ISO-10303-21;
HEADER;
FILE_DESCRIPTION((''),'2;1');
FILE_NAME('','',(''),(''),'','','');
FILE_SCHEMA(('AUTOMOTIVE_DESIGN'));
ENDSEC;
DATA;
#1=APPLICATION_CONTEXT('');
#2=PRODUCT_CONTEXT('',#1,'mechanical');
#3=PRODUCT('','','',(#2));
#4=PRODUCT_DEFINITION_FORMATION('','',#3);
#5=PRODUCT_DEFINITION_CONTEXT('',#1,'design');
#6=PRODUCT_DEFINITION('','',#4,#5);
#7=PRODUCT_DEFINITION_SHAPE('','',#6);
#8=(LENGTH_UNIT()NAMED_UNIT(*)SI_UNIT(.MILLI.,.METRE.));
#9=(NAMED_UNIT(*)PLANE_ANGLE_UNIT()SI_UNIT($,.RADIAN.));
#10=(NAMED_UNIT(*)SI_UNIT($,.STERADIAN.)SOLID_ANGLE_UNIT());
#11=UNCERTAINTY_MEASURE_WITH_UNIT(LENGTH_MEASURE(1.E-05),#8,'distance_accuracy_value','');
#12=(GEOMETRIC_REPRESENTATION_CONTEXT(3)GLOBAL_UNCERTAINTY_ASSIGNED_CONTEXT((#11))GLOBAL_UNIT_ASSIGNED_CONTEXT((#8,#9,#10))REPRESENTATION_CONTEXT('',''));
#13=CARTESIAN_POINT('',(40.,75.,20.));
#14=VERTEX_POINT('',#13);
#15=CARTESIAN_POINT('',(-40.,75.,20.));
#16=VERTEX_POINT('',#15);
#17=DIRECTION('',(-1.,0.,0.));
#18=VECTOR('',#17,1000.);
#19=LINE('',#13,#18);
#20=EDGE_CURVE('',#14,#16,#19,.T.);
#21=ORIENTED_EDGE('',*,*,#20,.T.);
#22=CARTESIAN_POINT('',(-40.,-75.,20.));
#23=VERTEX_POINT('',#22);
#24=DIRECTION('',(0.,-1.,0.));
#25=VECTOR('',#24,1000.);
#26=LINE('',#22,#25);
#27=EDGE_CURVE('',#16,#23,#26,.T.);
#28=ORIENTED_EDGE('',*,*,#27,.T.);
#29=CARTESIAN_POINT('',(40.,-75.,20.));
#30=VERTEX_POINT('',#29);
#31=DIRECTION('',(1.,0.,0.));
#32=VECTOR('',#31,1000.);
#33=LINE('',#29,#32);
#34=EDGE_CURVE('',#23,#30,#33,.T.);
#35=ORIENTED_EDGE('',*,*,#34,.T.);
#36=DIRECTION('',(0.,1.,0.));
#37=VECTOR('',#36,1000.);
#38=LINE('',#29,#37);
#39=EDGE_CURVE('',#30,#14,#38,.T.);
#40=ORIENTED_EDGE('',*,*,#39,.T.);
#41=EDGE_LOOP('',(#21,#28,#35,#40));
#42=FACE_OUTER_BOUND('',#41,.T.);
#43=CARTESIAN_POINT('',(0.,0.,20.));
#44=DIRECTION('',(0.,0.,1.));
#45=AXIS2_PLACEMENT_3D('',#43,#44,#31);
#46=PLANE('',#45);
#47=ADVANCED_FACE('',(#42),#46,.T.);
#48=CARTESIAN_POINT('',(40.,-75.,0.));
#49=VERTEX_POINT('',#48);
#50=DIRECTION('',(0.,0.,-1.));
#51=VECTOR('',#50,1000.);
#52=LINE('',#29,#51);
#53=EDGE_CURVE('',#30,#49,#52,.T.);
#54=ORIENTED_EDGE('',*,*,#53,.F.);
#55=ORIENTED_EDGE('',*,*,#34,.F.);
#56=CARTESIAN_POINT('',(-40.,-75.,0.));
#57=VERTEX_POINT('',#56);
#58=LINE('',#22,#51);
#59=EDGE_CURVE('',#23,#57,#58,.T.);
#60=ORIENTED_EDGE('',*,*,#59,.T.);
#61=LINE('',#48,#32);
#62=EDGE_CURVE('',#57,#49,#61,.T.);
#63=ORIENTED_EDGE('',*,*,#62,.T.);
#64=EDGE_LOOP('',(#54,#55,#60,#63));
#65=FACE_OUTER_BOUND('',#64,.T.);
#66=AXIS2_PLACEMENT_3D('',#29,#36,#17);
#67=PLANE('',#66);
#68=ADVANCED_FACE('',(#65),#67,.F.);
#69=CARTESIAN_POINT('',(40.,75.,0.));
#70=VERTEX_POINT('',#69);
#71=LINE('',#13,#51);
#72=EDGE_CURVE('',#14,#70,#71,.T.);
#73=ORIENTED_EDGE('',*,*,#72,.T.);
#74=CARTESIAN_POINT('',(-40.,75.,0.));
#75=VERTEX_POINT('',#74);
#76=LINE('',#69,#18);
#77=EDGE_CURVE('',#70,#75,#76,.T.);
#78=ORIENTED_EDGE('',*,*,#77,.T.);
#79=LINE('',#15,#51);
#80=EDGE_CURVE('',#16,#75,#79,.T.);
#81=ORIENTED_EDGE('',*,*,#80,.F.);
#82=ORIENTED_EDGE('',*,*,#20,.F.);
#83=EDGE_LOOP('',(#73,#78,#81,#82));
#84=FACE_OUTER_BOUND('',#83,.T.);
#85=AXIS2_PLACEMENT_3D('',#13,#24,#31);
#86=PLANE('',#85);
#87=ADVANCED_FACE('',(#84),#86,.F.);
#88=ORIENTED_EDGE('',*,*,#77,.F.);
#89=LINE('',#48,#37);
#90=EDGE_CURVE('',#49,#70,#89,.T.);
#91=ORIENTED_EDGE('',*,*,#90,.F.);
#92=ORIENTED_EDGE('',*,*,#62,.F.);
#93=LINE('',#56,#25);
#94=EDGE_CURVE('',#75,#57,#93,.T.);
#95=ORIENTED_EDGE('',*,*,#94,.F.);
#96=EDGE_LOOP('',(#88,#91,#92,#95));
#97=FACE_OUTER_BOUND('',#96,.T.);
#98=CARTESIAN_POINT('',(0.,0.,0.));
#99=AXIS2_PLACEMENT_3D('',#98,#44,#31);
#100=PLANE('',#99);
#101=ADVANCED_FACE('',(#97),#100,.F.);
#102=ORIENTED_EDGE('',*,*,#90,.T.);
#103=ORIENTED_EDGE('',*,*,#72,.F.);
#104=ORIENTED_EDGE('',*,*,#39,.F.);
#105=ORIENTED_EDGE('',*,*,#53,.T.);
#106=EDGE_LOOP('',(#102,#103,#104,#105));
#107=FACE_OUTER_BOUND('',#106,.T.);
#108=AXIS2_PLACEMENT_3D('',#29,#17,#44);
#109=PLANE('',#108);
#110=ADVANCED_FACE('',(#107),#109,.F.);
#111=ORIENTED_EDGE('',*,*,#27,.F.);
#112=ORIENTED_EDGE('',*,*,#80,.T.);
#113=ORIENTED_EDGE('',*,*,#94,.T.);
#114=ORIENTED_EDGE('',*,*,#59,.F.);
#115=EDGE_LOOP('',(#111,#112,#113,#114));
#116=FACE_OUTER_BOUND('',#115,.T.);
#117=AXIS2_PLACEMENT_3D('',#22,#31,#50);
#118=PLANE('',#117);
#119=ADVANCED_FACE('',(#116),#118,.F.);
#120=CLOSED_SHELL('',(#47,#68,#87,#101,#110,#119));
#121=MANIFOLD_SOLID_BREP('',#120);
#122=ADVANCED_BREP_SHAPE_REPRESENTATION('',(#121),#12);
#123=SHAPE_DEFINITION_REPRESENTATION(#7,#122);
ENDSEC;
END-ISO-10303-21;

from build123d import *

# Parameters (mm, degrees)
SKETCH1_W           = 80
SKETCH1_H           = 150
BOSS_EXTRUDE1_DEPTH = 20


with BuildPart() as part:
    # Sketch1 → Boss-Extrude1 (new body)
    with BuildSketch(Plane.XY):
        Rectangle(SKETCH1_W, SKETCH1_H)
    extrude(amount=BOSS_EXTRUDE1_DEPTH)


solid = part.part
